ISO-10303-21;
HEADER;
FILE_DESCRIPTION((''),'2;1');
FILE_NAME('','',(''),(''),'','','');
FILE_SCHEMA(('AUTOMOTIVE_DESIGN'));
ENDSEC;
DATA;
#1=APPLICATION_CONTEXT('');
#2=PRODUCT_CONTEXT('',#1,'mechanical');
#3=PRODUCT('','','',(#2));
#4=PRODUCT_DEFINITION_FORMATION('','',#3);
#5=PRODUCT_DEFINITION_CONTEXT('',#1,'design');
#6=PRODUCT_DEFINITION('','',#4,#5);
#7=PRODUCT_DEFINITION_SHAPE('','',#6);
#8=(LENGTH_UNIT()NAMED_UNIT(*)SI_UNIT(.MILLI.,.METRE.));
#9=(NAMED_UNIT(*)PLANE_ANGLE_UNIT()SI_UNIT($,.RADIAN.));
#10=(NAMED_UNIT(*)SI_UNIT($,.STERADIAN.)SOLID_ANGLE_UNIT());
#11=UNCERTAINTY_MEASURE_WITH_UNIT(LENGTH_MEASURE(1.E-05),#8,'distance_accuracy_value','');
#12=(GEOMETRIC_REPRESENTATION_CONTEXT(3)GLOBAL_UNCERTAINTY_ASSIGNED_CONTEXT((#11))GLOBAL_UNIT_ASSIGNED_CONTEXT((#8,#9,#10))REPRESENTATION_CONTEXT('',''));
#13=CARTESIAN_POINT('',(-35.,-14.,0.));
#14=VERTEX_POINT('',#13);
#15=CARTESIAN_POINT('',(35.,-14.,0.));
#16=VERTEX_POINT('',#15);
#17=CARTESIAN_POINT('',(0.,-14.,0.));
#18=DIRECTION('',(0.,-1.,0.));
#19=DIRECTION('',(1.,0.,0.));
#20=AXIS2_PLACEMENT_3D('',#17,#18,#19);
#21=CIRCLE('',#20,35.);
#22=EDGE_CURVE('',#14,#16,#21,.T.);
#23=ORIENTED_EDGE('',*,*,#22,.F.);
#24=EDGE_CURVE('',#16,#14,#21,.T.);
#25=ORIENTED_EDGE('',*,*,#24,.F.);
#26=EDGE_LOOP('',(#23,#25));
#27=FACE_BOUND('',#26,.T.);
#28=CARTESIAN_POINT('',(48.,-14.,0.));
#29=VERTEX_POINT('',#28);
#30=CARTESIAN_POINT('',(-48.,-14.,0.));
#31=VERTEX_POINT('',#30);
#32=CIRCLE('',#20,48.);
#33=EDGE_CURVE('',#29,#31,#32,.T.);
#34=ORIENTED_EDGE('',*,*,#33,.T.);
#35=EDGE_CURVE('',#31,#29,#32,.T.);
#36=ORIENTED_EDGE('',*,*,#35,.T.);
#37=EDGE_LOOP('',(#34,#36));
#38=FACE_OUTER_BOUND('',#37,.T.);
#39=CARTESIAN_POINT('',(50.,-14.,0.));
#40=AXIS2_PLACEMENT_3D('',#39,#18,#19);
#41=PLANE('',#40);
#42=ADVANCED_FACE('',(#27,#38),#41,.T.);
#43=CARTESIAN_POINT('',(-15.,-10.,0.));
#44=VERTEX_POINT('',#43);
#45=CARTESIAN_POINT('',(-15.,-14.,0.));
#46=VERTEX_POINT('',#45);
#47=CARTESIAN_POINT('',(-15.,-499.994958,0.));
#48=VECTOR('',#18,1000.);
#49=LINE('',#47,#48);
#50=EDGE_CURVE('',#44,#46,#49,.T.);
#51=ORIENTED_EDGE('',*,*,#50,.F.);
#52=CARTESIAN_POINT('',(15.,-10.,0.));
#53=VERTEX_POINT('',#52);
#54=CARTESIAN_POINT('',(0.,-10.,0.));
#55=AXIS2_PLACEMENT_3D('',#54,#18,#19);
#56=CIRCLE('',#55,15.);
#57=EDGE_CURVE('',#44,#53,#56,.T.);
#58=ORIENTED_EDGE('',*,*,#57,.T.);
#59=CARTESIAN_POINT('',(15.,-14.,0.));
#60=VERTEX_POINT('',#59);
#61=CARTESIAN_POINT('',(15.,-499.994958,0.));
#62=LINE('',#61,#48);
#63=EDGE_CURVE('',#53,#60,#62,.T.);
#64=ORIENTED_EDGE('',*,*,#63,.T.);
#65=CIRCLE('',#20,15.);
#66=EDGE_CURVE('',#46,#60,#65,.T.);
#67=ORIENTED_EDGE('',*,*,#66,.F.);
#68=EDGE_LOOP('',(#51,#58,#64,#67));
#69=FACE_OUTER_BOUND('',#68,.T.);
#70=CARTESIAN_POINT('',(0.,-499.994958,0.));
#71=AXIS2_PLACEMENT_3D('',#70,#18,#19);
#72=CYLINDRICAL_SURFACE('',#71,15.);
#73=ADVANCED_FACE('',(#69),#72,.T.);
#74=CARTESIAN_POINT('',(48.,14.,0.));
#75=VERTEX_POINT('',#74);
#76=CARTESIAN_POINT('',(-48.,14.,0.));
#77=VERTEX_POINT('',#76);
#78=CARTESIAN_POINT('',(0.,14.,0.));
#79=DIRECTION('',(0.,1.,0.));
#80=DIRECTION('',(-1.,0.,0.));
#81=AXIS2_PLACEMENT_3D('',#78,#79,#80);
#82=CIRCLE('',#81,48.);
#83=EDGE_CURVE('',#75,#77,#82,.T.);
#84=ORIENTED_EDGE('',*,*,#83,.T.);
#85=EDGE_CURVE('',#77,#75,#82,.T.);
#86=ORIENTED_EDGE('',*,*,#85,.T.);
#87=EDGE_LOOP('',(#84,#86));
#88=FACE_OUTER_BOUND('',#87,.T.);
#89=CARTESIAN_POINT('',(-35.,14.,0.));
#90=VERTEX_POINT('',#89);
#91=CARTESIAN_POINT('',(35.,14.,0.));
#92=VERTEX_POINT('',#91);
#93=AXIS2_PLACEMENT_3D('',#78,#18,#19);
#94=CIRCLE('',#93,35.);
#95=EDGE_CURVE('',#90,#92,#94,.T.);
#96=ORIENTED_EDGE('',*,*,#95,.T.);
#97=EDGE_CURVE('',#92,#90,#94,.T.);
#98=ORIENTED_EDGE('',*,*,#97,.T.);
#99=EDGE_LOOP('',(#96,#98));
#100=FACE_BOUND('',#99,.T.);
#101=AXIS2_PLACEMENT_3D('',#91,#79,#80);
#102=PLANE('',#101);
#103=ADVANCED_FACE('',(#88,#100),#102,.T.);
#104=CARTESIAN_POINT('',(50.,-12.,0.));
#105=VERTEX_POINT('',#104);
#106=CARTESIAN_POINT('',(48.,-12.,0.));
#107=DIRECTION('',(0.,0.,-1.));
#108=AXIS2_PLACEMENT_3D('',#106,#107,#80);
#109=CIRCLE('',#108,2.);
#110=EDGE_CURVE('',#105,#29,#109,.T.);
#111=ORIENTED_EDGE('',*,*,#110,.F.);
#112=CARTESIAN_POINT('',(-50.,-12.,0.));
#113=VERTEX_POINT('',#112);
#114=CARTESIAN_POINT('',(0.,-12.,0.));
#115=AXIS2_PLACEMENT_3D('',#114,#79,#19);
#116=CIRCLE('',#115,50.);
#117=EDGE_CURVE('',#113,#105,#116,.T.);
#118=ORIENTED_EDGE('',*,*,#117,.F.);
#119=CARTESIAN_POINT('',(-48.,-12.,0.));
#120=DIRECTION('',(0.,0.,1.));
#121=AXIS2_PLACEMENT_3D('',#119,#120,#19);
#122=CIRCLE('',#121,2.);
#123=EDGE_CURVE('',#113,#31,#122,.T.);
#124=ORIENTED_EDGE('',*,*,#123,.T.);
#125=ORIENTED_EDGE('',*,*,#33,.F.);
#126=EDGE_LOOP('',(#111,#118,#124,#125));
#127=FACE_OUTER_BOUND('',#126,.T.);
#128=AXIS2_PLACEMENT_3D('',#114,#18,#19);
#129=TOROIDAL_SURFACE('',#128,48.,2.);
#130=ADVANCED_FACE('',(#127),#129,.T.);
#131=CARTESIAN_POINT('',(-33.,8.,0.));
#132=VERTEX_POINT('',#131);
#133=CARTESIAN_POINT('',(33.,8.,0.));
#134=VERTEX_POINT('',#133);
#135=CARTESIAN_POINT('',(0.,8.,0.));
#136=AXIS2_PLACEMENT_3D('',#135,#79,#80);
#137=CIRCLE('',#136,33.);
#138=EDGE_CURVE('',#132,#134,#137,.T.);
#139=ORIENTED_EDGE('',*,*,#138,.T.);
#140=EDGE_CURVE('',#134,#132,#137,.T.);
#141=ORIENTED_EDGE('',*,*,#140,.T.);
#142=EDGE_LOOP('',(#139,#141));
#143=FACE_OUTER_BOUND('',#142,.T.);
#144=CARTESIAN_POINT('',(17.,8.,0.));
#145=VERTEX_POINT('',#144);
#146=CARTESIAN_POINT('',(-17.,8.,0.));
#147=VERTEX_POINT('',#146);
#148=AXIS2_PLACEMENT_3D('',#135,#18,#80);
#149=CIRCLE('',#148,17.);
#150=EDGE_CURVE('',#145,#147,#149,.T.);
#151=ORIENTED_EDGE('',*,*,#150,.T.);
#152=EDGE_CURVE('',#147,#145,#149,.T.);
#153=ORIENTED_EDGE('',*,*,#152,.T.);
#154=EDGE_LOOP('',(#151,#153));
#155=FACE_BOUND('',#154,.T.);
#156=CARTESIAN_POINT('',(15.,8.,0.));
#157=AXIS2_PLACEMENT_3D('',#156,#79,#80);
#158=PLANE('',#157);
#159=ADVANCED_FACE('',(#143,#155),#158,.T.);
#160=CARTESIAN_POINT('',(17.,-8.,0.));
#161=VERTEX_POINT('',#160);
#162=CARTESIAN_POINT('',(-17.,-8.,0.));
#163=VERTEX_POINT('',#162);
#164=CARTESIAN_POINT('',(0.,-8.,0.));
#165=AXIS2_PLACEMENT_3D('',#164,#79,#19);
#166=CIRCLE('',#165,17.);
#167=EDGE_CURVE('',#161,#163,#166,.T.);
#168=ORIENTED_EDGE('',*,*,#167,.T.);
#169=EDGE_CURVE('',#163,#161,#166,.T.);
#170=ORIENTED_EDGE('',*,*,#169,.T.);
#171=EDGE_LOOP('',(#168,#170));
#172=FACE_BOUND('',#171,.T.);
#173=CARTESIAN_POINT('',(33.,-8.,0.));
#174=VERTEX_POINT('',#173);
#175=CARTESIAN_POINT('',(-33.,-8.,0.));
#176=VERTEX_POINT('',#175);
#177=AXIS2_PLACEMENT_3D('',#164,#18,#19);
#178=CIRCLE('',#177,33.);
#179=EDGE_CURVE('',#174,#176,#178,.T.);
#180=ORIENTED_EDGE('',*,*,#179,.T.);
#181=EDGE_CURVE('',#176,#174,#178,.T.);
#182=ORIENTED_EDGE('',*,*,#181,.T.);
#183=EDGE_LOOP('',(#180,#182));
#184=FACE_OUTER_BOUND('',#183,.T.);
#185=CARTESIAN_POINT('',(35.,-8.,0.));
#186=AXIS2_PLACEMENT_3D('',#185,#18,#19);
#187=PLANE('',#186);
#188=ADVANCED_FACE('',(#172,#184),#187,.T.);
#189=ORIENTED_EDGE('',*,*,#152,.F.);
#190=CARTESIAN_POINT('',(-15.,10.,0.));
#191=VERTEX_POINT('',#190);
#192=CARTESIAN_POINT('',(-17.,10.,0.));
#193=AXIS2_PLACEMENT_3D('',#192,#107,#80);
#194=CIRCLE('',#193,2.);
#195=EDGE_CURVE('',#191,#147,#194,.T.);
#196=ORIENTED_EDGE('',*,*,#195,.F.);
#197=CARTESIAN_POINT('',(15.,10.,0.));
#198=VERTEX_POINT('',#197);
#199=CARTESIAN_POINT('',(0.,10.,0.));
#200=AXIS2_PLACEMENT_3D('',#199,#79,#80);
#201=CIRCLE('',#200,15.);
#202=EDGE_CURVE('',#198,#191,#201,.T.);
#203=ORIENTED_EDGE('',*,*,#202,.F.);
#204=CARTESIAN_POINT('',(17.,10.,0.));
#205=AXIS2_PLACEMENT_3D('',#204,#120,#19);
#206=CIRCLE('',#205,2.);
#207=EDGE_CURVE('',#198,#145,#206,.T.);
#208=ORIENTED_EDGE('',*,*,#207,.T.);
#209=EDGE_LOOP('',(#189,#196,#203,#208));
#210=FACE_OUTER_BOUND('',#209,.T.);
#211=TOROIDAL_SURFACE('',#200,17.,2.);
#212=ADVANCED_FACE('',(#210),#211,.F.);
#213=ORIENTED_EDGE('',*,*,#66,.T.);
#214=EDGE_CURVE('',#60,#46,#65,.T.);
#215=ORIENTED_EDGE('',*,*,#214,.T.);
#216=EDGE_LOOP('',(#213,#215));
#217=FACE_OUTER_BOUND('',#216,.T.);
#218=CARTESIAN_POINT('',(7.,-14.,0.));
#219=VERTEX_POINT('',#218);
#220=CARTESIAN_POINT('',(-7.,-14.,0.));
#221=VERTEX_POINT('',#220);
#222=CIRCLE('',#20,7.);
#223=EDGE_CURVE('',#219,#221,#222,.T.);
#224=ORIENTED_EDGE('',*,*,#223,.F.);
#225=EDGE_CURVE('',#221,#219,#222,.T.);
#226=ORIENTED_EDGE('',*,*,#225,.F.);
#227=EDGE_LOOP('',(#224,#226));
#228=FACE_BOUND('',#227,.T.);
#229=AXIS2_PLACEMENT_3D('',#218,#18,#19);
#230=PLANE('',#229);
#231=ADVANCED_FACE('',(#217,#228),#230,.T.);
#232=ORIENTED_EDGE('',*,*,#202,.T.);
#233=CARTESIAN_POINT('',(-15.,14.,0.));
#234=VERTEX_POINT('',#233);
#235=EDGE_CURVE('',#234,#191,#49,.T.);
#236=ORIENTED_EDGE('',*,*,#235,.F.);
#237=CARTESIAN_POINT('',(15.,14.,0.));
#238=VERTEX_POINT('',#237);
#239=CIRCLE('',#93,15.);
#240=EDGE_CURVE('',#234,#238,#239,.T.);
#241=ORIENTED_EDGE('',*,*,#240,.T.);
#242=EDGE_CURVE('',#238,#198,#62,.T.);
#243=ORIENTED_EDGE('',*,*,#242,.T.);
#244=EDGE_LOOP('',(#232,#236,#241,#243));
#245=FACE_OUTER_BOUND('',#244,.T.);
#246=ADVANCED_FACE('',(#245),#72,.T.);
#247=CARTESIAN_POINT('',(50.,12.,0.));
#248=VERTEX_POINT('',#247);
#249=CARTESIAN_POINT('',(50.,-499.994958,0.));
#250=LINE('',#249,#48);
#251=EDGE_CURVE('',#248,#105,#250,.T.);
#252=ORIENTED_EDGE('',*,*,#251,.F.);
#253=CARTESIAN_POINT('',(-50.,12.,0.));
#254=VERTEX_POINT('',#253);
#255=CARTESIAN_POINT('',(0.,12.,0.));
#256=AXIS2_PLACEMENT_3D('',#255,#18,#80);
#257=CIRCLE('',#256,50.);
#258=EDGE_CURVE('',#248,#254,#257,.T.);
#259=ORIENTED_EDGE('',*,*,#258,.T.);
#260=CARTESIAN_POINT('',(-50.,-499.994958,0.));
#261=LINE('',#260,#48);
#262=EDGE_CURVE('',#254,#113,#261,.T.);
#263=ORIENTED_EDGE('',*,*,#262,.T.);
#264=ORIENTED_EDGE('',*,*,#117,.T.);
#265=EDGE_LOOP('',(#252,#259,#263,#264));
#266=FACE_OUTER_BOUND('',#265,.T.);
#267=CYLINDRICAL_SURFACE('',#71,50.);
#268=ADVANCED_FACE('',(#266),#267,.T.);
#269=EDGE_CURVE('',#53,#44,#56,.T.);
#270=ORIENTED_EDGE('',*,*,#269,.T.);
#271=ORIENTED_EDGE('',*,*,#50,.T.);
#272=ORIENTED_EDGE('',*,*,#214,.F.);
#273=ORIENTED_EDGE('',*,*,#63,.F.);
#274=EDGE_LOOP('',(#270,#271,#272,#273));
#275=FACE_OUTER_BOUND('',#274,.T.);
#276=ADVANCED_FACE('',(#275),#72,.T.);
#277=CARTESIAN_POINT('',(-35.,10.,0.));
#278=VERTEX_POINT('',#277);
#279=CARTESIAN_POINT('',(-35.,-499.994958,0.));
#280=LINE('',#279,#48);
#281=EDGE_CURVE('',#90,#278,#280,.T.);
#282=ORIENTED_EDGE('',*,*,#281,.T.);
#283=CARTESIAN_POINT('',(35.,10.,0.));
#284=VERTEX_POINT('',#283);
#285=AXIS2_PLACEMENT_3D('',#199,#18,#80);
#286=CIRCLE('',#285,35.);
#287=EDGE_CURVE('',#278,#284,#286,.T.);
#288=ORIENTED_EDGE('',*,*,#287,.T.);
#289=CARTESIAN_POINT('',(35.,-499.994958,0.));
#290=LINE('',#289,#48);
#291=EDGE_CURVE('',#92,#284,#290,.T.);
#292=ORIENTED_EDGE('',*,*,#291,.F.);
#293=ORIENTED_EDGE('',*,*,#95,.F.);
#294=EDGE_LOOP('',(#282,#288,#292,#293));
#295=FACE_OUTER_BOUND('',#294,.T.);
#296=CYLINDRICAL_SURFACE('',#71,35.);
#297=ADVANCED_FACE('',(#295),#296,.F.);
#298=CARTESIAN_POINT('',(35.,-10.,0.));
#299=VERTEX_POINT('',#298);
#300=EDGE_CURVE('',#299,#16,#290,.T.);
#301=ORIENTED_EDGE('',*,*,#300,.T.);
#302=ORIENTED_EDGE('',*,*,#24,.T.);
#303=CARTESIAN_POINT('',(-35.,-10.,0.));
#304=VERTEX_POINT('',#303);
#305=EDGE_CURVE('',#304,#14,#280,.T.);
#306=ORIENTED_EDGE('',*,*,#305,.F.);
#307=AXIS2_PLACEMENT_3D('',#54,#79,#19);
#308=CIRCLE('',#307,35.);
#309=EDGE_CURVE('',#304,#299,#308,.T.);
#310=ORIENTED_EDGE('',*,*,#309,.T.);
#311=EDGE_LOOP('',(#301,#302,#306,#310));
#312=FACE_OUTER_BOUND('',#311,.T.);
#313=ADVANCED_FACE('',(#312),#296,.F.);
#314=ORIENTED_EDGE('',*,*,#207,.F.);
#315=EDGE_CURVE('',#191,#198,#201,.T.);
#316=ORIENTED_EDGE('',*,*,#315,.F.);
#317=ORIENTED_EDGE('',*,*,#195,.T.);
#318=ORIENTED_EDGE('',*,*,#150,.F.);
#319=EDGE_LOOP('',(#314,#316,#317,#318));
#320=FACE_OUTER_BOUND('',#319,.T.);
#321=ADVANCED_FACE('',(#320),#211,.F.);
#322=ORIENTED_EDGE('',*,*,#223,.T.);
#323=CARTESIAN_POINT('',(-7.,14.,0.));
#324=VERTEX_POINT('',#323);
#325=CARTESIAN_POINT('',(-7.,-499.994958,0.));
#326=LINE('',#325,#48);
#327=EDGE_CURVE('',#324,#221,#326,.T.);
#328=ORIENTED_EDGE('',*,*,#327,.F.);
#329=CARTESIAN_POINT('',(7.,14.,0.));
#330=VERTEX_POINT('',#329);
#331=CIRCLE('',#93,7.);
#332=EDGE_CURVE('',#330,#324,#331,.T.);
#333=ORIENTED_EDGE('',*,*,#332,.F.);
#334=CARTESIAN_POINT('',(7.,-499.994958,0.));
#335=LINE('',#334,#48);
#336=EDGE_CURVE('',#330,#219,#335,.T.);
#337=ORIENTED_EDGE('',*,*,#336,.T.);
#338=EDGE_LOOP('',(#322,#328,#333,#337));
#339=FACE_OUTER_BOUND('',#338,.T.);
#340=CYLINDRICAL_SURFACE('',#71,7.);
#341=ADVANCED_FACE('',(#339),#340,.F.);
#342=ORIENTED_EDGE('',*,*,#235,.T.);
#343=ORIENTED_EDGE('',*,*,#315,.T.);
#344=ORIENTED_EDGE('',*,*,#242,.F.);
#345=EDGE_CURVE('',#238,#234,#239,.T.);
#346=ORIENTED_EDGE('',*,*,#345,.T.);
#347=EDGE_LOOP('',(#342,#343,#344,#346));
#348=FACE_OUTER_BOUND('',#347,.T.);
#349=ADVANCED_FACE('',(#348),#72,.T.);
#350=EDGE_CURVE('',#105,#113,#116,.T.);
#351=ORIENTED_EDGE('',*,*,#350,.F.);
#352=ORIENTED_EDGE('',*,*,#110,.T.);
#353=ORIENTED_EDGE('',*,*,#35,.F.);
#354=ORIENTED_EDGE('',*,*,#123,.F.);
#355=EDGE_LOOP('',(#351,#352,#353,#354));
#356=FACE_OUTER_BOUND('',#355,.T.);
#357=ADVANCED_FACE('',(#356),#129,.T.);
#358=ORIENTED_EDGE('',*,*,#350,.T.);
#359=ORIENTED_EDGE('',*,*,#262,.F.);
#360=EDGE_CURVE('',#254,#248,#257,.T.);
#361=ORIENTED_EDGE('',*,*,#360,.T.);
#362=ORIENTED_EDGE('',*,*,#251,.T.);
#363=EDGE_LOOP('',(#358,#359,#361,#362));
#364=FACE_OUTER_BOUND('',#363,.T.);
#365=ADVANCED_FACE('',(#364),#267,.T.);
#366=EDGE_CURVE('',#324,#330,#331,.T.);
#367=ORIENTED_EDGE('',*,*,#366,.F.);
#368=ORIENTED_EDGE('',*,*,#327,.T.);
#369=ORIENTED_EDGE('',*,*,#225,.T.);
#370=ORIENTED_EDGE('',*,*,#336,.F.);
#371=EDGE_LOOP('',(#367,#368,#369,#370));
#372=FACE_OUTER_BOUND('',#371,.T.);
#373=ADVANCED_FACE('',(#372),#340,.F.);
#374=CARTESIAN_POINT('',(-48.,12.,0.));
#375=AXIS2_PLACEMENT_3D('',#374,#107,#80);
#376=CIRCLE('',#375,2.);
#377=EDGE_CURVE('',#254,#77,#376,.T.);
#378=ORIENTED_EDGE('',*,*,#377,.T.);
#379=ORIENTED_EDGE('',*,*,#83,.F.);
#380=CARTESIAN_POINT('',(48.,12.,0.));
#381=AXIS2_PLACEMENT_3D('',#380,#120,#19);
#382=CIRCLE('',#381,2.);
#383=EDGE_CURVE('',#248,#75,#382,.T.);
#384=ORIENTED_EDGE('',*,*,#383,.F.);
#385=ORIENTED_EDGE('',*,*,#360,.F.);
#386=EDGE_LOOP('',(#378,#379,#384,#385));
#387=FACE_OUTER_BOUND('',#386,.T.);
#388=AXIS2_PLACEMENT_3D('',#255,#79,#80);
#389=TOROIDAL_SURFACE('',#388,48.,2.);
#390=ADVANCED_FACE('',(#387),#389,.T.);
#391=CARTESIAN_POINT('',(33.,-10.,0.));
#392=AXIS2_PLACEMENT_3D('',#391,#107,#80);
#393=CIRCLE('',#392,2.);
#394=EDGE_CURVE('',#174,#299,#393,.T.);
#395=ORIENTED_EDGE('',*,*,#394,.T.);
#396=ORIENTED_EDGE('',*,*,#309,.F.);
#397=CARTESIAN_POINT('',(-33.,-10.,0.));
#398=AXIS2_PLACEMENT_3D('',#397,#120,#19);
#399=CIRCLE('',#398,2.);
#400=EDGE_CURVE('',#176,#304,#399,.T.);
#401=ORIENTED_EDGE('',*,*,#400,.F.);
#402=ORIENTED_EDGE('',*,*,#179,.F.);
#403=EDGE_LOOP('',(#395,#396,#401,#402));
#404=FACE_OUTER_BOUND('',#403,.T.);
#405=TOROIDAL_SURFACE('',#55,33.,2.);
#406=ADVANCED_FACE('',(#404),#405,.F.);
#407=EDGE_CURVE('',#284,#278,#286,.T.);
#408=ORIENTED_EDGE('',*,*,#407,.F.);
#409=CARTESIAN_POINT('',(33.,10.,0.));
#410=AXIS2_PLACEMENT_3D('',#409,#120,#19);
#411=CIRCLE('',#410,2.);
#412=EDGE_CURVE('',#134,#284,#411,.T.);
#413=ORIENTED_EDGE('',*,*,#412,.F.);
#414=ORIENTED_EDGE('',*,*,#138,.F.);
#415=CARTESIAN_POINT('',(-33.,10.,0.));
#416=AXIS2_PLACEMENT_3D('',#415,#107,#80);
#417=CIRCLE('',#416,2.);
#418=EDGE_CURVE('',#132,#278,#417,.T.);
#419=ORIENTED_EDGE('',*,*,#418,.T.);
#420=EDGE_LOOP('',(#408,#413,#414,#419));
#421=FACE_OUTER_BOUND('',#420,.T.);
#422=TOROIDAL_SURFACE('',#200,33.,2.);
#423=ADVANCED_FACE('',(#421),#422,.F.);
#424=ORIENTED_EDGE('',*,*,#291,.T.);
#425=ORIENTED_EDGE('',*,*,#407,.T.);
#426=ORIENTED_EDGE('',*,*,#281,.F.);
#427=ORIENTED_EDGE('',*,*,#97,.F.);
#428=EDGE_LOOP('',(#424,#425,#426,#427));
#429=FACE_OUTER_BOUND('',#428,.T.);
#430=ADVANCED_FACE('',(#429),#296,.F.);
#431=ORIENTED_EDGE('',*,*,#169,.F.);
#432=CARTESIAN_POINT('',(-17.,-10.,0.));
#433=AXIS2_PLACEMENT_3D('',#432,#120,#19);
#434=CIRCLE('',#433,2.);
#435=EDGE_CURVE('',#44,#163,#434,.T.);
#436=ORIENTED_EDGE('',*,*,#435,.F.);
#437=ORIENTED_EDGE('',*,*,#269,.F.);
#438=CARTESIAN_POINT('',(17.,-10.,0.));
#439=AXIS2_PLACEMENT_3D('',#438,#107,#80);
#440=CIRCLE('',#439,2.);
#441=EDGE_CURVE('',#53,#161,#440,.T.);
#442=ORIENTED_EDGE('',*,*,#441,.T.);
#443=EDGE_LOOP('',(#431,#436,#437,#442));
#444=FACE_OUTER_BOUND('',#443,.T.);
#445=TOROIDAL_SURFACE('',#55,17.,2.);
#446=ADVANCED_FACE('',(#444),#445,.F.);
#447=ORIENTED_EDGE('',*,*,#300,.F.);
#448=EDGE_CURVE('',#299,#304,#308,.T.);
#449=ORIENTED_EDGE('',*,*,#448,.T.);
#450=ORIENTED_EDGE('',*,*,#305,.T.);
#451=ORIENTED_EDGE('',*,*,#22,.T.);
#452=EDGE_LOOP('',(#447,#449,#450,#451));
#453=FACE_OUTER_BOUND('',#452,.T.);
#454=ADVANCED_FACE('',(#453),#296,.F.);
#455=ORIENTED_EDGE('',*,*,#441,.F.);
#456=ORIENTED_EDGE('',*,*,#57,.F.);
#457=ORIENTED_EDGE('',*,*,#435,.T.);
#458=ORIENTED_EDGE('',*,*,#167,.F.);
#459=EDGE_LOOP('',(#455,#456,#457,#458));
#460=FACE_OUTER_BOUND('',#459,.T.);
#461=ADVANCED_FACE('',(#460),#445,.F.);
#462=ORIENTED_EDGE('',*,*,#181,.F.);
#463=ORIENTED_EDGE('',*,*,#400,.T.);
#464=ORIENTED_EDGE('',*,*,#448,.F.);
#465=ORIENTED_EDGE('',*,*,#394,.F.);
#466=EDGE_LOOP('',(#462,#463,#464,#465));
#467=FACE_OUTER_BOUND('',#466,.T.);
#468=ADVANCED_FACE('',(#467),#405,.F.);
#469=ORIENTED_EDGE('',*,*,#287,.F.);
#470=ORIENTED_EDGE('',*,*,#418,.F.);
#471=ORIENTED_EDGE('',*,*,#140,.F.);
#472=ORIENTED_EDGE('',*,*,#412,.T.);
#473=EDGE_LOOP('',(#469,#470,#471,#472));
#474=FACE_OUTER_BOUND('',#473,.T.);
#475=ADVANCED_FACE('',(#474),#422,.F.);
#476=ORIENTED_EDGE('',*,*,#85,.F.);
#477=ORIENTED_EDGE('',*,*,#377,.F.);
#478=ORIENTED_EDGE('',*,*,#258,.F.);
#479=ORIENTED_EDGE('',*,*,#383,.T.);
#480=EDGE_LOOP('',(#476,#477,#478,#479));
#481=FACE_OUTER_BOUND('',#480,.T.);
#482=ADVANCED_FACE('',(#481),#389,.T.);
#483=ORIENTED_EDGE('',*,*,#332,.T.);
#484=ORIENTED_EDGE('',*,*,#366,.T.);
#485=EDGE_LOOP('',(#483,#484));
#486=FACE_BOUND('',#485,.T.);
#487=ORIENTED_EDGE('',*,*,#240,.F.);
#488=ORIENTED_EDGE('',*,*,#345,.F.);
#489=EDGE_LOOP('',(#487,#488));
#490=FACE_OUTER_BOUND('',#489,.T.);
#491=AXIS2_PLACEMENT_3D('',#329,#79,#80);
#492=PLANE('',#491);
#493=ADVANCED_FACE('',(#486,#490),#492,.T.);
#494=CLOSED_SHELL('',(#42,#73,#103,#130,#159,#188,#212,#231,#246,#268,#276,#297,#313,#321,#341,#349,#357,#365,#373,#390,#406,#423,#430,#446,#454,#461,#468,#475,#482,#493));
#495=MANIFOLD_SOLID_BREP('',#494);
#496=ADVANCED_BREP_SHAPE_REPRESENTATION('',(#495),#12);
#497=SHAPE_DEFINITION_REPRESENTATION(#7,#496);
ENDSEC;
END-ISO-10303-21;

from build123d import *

# Parameters (mm, degrees)
FILLET2_R = 2
FILLET4_R = 2


with BuildPart() as part:
    # Sketch1 → Revolve1 (revolve)
    with BuildSketch(Plane.XY):
        Polygon((15, 8), (35, 8), (35, 14), (50, 14), (50, -14), (35, -14), (35, -8), (15, -8), (15, -14), (7, -14), (7, 14), (15, 14), align=None)
    revolve(axis=Axis((0, -499.994958486, 0), (0, 1, 0)))

    # Fillet2
    fillet2_edges = [part.edges().sort_by_distance(p)[0] for p in [
        (-15, 8, 0),
        (-35, 8, 0),
        (-50, 14, 0),
    ]]
    fillet(fillet2_edges, radius=FILLET2_R)

    # Fillet4
    fillet4_edges = [part.edges().sort_by_distance(p)[0] for p in [
        (-50, -14, 0),
        (-35, -8, 0),
        (-15, -8, 0),
    ]]
    fillet(fillet4_edges, radius=FILLET4_R)


solid = part.part
